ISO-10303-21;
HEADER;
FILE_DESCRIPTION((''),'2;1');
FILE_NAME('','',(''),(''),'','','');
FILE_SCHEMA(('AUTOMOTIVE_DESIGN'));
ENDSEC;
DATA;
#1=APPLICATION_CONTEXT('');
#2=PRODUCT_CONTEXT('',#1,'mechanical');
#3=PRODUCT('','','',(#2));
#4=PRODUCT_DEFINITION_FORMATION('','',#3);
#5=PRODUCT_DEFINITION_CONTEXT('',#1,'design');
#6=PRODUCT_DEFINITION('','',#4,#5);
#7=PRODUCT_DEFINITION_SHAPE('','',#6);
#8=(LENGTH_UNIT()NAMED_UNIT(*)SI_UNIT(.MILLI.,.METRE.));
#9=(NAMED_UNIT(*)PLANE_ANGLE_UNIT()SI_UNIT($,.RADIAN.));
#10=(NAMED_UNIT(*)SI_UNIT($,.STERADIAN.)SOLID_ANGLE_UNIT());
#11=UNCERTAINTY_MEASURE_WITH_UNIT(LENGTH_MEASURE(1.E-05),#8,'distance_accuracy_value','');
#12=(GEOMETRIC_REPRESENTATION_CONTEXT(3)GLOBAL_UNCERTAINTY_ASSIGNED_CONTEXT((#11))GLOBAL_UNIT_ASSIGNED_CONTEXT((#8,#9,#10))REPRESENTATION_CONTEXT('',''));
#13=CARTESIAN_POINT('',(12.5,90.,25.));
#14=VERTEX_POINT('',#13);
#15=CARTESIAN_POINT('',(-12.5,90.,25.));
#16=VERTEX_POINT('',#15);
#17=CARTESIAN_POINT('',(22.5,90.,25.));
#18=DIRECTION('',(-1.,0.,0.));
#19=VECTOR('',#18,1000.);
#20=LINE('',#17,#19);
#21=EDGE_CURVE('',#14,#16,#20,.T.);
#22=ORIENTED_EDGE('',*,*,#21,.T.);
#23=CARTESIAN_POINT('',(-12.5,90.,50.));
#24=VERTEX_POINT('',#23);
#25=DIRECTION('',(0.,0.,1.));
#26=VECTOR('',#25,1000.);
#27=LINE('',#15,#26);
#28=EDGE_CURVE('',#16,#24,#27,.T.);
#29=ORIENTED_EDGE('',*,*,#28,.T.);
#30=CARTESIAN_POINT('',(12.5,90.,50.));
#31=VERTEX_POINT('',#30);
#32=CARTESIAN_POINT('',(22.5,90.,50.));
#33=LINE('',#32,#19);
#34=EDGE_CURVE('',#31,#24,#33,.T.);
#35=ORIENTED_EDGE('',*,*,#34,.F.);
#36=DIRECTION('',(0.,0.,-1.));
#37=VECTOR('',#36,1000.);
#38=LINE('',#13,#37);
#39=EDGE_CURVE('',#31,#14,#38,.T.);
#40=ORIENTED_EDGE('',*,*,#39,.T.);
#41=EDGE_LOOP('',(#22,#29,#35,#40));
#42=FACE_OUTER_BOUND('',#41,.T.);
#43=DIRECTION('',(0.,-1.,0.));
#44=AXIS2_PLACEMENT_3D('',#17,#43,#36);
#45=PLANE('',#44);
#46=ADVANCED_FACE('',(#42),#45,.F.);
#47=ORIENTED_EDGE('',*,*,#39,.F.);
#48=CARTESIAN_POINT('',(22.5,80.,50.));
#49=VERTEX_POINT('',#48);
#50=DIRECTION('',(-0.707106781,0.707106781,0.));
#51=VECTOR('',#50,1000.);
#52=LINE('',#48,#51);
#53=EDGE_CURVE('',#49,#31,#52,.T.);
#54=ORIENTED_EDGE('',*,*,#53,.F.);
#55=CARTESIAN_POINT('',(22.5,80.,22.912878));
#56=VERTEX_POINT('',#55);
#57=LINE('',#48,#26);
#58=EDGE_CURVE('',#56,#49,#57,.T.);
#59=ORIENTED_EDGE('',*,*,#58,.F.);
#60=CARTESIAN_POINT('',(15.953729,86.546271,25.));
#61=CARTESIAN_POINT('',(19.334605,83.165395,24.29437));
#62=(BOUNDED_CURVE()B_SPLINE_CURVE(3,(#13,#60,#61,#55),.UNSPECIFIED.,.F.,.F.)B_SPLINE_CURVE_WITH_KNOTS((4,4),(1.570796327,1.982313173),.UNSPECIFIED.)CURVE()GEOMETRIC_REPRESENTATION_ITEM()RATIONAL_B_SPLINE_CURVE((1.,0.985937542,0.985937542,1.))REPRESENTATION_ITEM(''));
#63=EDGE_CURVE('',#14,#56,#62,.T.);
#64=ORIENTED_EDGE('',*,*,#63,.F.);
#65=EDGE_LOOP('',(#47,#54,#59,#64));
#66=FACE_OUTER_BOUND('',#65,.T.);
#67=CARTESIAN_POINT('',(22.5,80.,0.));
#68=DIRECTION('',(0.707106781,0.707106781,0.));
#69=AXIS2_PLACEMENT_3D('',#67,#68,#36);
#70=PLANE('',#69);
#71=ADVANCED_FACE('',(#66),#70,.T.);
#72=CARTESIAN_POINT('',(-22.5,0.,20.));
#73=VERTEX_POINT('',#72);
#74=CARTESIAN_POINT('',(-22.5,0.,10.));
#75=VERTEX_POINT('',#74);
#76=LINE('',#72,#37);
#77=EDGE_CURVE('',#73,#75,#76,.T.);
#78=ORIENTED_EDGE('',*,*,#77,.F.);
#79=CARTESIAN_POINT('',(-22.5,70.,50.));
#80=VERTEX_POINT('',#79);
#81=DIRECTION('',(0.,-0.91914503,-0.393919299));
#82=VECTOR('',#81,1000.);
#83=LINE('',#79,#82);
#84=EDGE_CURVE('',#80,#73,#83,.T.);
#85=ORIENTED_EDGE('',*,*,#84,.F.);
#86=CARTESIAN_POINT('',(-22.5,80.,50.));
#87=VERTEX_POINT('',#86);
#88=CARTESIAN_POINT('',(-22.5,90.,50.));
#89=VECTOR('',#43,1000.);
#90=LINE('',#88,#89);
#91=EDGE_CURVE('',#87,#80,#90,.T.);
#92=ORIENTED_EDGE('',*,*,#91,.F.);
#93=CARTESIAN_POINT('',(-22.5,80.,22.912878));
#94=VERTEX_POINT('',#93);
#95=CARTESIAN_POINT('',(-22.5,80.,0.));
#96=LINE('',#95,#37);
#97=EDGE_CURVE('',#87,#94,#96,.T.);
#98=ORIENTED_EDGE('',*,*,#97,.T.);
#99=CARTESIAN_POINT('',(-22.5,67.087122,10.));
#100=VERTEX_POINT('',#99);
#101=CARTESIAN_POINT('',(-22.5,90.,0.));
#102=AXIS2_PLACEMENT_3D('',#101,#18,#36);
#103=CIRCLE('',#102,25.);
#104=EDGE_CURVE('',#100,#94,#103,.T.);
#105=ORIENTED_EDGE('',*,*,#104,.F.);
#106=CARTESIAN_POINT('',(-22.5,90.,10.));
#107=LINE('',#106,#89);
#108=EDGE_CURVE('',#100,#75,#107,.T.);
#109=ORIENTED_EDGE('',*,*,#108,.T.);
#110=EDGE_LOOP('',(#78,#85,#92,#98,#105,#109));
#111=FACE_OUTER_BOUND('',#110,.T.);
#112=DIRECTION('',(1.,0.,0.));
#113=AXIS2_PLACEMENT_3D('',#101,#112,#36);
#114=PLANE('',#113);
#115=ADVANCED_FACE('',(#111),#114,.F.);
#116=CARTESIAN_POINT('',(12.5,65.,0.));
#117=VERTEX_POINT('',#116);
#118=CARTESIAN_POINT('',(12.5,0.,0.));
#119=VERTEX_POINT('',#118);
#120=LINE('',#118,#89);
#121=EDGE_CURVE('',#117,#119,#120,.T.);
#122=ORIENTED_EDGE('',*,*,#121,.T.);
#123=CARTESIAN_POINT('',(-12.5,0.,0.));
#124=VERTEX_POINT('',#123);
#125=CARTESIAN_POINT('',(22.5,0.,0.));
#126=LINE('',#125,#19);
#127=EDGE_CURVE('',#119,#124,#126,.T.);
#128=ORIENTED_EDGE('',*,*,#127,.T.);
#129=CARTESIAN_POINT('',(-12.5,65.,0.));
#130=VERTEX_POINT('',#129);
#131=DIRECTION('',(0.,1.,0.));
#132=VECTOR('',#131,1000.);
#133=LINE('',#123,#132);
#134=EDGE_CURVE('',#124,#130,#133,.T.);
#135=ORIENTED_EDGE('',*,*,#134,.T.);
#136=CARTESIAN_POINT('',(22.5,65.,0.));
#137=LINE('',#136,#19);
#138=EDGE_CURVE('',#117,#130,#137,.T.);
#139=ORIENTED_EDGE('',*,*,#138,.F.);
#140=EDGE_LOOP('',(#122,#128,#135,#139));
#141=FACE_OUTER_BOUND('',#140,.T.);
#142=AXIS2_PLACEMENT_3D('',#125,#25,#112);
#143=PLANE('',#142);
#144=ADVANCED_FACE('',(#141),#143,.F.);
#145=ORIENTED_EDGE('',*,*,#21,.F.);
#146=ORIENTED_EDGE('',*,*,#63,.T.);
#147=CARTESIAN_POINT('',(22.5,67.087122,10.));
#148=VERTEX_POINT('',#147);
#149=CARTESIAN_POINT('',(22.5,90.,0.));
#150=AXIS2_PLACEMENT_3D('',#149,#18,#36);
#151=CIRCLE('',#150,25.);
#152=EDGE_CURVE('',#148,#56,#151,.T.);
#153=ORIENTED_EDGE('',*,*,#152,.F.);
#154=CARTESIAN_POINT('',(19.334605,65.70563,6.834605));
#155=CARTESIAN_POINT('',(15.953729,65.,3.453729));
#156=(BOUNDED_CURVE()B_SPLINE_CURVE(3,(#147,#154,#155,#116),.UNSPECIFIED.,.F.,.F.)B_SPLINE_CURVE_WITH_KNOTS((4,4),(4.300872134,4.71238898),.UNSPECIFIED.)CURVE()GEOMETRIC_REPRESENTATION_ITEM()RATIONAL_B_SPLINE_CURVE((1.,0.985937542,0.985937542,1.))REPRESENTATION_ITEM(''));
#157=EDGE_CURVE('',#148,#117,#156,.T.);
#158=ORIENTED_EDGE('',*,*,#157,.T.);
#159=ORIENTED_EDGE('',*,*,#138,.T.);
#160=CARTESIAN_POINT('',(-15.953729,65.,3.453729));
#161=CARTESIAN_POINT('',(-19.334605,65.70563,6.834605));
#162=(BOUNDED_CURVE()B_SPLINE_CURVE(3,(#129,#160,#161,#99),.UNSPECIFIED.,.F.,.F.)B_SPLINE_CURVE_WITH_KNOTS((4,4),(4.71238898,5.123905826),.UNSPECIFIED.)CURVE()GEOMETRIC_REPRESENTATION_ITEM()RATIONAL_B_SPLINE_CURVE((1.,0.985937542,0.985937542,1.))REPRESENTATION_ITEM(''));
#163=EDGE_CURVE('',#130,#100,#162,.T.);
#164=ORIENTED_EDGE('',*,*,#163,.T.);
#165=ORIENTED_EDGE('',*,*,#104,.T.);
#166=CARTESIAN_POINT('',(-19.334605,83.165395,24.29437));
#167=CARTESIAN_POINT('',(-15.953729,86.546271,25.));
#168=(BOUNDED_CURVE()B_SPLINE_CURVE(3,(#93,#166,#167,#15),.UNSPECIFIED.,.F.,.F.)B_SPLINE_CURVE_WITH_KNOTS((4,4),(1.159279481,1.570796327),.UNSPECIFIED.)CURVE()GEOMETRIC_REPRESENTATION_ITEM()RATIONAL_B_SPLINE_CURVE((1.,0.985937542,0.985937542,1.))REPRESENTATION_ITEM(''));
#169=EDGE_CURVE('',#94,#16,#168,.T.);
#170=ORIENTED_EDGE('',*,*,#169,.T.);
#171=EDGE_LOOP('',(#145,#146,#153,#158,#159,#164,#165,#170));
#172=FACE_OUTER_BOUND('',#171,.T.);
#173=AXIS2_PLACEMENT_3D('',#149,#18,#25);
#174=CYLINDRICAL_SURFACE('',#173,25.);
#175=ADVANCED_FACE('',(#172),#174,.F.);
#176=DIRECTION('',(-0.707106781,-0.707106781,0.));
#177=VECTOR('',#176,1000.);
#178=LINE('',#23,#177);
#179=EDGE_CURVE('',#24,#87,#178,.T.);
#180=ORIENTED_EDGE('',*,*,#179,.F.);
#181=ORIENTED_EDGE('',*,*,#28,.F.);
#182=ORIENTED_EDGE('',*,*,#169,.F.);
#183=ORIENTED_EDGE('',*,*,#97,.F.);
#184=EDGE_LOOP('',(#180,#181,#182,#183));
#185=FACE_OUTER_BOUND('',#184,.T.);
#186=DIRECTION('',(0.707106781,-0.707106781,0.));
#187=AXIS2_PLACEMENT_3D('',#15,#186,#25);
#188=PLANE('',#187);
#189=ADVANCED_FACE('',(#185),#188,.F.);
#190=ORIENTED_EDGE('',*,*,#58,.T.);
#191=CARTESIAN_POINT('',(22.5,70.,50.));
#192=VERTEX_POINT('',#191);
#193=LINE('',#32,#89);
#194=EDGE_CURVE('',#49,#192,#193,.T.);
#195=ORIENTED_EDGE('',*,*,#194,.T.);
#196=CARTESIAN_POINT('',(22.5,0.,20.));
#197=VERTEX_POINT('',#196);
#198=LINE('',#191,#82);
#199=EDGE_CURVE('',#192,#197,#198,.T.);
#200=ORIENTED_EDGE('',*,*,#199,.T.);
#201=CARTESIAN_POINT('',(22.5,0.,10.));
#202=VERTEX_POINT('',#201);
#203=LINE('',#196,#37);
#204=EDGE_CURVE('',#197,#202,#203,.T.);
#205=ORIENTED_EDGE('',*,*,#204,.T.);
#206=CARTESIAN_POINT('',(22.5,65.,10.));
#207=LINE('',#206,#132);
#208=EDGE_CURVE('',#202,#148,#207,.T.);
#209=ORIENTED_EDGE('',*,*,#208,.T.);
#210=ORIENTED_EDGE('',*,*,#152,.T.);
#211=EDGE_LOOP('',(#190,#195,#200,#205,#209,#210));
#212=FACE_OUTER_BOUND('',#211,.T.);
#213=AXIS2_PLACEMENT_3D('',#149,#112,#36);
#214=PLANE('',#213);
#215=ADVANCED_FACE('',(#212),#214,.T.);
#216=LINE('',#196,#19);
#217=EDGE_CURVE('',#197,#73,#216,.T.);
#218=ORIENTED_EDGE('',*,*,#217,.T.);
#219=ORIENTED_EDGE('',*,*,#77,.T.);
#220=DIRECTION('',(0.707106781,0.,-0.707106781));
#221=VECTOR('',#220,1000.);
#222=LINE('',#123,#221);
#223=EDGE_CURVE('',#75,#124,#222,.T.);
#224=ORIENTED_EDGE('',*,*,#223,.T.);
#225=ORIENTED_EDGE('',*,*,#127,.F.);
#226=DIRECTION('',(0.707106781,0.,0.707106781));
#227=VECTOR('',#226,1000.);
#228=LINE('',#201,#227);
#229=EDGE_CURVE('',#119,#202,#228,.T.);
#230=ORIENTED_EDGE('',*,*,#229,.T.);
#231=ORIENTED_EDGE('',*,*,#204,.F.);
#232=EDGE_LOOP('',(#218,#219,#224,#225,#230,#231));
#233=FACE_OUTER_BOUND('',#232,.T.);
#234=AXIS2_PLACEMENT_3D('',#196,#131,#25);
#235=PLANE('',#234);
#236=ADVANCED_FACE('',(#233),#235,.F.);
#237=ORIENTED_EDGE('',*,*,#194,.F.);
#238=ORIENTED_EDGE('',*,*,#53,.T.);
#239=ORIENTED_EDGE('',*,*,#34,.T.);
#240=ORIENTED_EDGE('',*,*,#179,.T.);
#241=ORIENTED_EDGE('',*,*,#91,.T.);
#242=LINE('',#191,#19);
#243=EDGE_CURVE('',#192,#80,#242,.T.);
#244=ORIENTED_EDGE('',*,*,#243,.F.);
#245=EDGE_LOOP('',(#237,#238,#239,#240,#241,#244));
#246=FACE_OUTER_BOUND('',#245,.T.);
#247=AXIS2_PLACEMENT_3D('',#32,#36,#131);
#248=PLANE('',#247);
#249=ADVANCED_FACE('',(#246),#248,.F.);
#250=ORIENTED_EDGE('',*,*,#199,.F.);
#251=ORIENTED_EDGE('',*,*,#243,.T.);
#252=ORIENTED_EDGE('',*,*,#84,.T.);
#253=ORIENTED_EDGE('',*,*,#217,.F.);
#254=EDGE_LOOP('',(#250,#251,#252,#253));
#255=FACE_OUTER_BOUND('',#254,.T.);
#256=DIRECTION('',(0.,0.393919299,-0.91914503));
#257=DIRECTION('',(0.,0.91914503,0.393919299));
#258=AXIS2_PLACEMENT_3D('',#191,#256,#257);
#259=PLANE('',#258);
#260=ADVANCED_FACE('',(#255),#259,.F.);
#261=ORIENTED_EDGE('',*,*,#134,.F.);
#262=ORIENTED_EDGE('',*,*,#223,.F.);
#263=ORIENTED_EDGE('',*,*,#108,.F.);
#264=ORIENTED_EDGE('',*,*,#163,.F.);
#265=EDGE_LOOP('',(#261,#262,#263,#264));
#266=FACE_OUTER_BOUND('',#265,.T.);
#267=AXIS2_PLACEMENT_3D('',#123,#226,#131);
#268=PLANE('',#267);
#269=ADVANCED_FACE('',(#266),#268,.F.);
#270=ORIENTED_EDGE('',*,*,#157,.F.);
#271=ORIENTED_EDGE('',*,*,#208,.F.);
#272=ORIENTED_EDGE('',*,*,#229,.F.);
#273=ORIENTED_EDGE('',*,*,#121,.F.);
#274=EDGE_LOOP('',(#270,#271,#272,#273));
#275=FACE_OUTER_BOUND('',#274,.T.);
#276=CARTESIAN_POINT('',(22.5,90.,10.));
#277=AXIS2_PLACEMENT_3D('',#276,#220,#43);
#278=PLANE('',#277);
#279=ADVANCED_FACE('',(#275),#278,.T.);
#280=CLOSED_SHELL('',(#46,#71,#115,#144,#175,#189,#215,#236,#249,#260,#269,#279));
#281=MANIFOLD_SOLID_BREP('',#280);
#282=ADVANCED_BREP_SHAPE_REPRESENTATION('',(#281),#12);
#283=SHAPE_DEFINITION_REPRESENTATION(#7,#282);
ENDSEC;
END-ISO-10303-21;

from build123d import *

# Parameters (mm, degrees)
BOSS_EXTRUDE1_DEPTH = 22.5
CHAMFER1_SIZE       = 10


with BuildPart() as part:
    # Sketch1 → Boss-Extrude1 (new, symmetric)
    with BuildSketch(Plane(origin=(0, 0, 0), x_dir=(0, 0, -1), z_dir=(1, 0, 0))):
        with BuildLine():
            Line((0, 0), (0, 65))
            ThreePointArc((0, 65), (-17.67766953, 72.32233047), (-25, 90))
            Line((-25, 90), (-50, 90))
            Line((-50, 90), (-50, 70))
            Line((-50, 70), (-20, 0))
            Line((-20, 0), (0, 0))
        make_face()
    extrude(amount=BOSS_EXTRUDE1_DEPTH, both=True)

    # Chamfer1
    chamfer1_edges = [part.edges().sort_by_distance(p)[0] for p in [
        (22.5, 90, 37.5),
        (-22.5, 90, 37.5),
        (22.5, 32.5, 0),
        (-22.5, 32.5, 0),
    ]]
    chamfer(chamfer1_edges, length=CHAMFER1_SIZE)


solid = part.part
